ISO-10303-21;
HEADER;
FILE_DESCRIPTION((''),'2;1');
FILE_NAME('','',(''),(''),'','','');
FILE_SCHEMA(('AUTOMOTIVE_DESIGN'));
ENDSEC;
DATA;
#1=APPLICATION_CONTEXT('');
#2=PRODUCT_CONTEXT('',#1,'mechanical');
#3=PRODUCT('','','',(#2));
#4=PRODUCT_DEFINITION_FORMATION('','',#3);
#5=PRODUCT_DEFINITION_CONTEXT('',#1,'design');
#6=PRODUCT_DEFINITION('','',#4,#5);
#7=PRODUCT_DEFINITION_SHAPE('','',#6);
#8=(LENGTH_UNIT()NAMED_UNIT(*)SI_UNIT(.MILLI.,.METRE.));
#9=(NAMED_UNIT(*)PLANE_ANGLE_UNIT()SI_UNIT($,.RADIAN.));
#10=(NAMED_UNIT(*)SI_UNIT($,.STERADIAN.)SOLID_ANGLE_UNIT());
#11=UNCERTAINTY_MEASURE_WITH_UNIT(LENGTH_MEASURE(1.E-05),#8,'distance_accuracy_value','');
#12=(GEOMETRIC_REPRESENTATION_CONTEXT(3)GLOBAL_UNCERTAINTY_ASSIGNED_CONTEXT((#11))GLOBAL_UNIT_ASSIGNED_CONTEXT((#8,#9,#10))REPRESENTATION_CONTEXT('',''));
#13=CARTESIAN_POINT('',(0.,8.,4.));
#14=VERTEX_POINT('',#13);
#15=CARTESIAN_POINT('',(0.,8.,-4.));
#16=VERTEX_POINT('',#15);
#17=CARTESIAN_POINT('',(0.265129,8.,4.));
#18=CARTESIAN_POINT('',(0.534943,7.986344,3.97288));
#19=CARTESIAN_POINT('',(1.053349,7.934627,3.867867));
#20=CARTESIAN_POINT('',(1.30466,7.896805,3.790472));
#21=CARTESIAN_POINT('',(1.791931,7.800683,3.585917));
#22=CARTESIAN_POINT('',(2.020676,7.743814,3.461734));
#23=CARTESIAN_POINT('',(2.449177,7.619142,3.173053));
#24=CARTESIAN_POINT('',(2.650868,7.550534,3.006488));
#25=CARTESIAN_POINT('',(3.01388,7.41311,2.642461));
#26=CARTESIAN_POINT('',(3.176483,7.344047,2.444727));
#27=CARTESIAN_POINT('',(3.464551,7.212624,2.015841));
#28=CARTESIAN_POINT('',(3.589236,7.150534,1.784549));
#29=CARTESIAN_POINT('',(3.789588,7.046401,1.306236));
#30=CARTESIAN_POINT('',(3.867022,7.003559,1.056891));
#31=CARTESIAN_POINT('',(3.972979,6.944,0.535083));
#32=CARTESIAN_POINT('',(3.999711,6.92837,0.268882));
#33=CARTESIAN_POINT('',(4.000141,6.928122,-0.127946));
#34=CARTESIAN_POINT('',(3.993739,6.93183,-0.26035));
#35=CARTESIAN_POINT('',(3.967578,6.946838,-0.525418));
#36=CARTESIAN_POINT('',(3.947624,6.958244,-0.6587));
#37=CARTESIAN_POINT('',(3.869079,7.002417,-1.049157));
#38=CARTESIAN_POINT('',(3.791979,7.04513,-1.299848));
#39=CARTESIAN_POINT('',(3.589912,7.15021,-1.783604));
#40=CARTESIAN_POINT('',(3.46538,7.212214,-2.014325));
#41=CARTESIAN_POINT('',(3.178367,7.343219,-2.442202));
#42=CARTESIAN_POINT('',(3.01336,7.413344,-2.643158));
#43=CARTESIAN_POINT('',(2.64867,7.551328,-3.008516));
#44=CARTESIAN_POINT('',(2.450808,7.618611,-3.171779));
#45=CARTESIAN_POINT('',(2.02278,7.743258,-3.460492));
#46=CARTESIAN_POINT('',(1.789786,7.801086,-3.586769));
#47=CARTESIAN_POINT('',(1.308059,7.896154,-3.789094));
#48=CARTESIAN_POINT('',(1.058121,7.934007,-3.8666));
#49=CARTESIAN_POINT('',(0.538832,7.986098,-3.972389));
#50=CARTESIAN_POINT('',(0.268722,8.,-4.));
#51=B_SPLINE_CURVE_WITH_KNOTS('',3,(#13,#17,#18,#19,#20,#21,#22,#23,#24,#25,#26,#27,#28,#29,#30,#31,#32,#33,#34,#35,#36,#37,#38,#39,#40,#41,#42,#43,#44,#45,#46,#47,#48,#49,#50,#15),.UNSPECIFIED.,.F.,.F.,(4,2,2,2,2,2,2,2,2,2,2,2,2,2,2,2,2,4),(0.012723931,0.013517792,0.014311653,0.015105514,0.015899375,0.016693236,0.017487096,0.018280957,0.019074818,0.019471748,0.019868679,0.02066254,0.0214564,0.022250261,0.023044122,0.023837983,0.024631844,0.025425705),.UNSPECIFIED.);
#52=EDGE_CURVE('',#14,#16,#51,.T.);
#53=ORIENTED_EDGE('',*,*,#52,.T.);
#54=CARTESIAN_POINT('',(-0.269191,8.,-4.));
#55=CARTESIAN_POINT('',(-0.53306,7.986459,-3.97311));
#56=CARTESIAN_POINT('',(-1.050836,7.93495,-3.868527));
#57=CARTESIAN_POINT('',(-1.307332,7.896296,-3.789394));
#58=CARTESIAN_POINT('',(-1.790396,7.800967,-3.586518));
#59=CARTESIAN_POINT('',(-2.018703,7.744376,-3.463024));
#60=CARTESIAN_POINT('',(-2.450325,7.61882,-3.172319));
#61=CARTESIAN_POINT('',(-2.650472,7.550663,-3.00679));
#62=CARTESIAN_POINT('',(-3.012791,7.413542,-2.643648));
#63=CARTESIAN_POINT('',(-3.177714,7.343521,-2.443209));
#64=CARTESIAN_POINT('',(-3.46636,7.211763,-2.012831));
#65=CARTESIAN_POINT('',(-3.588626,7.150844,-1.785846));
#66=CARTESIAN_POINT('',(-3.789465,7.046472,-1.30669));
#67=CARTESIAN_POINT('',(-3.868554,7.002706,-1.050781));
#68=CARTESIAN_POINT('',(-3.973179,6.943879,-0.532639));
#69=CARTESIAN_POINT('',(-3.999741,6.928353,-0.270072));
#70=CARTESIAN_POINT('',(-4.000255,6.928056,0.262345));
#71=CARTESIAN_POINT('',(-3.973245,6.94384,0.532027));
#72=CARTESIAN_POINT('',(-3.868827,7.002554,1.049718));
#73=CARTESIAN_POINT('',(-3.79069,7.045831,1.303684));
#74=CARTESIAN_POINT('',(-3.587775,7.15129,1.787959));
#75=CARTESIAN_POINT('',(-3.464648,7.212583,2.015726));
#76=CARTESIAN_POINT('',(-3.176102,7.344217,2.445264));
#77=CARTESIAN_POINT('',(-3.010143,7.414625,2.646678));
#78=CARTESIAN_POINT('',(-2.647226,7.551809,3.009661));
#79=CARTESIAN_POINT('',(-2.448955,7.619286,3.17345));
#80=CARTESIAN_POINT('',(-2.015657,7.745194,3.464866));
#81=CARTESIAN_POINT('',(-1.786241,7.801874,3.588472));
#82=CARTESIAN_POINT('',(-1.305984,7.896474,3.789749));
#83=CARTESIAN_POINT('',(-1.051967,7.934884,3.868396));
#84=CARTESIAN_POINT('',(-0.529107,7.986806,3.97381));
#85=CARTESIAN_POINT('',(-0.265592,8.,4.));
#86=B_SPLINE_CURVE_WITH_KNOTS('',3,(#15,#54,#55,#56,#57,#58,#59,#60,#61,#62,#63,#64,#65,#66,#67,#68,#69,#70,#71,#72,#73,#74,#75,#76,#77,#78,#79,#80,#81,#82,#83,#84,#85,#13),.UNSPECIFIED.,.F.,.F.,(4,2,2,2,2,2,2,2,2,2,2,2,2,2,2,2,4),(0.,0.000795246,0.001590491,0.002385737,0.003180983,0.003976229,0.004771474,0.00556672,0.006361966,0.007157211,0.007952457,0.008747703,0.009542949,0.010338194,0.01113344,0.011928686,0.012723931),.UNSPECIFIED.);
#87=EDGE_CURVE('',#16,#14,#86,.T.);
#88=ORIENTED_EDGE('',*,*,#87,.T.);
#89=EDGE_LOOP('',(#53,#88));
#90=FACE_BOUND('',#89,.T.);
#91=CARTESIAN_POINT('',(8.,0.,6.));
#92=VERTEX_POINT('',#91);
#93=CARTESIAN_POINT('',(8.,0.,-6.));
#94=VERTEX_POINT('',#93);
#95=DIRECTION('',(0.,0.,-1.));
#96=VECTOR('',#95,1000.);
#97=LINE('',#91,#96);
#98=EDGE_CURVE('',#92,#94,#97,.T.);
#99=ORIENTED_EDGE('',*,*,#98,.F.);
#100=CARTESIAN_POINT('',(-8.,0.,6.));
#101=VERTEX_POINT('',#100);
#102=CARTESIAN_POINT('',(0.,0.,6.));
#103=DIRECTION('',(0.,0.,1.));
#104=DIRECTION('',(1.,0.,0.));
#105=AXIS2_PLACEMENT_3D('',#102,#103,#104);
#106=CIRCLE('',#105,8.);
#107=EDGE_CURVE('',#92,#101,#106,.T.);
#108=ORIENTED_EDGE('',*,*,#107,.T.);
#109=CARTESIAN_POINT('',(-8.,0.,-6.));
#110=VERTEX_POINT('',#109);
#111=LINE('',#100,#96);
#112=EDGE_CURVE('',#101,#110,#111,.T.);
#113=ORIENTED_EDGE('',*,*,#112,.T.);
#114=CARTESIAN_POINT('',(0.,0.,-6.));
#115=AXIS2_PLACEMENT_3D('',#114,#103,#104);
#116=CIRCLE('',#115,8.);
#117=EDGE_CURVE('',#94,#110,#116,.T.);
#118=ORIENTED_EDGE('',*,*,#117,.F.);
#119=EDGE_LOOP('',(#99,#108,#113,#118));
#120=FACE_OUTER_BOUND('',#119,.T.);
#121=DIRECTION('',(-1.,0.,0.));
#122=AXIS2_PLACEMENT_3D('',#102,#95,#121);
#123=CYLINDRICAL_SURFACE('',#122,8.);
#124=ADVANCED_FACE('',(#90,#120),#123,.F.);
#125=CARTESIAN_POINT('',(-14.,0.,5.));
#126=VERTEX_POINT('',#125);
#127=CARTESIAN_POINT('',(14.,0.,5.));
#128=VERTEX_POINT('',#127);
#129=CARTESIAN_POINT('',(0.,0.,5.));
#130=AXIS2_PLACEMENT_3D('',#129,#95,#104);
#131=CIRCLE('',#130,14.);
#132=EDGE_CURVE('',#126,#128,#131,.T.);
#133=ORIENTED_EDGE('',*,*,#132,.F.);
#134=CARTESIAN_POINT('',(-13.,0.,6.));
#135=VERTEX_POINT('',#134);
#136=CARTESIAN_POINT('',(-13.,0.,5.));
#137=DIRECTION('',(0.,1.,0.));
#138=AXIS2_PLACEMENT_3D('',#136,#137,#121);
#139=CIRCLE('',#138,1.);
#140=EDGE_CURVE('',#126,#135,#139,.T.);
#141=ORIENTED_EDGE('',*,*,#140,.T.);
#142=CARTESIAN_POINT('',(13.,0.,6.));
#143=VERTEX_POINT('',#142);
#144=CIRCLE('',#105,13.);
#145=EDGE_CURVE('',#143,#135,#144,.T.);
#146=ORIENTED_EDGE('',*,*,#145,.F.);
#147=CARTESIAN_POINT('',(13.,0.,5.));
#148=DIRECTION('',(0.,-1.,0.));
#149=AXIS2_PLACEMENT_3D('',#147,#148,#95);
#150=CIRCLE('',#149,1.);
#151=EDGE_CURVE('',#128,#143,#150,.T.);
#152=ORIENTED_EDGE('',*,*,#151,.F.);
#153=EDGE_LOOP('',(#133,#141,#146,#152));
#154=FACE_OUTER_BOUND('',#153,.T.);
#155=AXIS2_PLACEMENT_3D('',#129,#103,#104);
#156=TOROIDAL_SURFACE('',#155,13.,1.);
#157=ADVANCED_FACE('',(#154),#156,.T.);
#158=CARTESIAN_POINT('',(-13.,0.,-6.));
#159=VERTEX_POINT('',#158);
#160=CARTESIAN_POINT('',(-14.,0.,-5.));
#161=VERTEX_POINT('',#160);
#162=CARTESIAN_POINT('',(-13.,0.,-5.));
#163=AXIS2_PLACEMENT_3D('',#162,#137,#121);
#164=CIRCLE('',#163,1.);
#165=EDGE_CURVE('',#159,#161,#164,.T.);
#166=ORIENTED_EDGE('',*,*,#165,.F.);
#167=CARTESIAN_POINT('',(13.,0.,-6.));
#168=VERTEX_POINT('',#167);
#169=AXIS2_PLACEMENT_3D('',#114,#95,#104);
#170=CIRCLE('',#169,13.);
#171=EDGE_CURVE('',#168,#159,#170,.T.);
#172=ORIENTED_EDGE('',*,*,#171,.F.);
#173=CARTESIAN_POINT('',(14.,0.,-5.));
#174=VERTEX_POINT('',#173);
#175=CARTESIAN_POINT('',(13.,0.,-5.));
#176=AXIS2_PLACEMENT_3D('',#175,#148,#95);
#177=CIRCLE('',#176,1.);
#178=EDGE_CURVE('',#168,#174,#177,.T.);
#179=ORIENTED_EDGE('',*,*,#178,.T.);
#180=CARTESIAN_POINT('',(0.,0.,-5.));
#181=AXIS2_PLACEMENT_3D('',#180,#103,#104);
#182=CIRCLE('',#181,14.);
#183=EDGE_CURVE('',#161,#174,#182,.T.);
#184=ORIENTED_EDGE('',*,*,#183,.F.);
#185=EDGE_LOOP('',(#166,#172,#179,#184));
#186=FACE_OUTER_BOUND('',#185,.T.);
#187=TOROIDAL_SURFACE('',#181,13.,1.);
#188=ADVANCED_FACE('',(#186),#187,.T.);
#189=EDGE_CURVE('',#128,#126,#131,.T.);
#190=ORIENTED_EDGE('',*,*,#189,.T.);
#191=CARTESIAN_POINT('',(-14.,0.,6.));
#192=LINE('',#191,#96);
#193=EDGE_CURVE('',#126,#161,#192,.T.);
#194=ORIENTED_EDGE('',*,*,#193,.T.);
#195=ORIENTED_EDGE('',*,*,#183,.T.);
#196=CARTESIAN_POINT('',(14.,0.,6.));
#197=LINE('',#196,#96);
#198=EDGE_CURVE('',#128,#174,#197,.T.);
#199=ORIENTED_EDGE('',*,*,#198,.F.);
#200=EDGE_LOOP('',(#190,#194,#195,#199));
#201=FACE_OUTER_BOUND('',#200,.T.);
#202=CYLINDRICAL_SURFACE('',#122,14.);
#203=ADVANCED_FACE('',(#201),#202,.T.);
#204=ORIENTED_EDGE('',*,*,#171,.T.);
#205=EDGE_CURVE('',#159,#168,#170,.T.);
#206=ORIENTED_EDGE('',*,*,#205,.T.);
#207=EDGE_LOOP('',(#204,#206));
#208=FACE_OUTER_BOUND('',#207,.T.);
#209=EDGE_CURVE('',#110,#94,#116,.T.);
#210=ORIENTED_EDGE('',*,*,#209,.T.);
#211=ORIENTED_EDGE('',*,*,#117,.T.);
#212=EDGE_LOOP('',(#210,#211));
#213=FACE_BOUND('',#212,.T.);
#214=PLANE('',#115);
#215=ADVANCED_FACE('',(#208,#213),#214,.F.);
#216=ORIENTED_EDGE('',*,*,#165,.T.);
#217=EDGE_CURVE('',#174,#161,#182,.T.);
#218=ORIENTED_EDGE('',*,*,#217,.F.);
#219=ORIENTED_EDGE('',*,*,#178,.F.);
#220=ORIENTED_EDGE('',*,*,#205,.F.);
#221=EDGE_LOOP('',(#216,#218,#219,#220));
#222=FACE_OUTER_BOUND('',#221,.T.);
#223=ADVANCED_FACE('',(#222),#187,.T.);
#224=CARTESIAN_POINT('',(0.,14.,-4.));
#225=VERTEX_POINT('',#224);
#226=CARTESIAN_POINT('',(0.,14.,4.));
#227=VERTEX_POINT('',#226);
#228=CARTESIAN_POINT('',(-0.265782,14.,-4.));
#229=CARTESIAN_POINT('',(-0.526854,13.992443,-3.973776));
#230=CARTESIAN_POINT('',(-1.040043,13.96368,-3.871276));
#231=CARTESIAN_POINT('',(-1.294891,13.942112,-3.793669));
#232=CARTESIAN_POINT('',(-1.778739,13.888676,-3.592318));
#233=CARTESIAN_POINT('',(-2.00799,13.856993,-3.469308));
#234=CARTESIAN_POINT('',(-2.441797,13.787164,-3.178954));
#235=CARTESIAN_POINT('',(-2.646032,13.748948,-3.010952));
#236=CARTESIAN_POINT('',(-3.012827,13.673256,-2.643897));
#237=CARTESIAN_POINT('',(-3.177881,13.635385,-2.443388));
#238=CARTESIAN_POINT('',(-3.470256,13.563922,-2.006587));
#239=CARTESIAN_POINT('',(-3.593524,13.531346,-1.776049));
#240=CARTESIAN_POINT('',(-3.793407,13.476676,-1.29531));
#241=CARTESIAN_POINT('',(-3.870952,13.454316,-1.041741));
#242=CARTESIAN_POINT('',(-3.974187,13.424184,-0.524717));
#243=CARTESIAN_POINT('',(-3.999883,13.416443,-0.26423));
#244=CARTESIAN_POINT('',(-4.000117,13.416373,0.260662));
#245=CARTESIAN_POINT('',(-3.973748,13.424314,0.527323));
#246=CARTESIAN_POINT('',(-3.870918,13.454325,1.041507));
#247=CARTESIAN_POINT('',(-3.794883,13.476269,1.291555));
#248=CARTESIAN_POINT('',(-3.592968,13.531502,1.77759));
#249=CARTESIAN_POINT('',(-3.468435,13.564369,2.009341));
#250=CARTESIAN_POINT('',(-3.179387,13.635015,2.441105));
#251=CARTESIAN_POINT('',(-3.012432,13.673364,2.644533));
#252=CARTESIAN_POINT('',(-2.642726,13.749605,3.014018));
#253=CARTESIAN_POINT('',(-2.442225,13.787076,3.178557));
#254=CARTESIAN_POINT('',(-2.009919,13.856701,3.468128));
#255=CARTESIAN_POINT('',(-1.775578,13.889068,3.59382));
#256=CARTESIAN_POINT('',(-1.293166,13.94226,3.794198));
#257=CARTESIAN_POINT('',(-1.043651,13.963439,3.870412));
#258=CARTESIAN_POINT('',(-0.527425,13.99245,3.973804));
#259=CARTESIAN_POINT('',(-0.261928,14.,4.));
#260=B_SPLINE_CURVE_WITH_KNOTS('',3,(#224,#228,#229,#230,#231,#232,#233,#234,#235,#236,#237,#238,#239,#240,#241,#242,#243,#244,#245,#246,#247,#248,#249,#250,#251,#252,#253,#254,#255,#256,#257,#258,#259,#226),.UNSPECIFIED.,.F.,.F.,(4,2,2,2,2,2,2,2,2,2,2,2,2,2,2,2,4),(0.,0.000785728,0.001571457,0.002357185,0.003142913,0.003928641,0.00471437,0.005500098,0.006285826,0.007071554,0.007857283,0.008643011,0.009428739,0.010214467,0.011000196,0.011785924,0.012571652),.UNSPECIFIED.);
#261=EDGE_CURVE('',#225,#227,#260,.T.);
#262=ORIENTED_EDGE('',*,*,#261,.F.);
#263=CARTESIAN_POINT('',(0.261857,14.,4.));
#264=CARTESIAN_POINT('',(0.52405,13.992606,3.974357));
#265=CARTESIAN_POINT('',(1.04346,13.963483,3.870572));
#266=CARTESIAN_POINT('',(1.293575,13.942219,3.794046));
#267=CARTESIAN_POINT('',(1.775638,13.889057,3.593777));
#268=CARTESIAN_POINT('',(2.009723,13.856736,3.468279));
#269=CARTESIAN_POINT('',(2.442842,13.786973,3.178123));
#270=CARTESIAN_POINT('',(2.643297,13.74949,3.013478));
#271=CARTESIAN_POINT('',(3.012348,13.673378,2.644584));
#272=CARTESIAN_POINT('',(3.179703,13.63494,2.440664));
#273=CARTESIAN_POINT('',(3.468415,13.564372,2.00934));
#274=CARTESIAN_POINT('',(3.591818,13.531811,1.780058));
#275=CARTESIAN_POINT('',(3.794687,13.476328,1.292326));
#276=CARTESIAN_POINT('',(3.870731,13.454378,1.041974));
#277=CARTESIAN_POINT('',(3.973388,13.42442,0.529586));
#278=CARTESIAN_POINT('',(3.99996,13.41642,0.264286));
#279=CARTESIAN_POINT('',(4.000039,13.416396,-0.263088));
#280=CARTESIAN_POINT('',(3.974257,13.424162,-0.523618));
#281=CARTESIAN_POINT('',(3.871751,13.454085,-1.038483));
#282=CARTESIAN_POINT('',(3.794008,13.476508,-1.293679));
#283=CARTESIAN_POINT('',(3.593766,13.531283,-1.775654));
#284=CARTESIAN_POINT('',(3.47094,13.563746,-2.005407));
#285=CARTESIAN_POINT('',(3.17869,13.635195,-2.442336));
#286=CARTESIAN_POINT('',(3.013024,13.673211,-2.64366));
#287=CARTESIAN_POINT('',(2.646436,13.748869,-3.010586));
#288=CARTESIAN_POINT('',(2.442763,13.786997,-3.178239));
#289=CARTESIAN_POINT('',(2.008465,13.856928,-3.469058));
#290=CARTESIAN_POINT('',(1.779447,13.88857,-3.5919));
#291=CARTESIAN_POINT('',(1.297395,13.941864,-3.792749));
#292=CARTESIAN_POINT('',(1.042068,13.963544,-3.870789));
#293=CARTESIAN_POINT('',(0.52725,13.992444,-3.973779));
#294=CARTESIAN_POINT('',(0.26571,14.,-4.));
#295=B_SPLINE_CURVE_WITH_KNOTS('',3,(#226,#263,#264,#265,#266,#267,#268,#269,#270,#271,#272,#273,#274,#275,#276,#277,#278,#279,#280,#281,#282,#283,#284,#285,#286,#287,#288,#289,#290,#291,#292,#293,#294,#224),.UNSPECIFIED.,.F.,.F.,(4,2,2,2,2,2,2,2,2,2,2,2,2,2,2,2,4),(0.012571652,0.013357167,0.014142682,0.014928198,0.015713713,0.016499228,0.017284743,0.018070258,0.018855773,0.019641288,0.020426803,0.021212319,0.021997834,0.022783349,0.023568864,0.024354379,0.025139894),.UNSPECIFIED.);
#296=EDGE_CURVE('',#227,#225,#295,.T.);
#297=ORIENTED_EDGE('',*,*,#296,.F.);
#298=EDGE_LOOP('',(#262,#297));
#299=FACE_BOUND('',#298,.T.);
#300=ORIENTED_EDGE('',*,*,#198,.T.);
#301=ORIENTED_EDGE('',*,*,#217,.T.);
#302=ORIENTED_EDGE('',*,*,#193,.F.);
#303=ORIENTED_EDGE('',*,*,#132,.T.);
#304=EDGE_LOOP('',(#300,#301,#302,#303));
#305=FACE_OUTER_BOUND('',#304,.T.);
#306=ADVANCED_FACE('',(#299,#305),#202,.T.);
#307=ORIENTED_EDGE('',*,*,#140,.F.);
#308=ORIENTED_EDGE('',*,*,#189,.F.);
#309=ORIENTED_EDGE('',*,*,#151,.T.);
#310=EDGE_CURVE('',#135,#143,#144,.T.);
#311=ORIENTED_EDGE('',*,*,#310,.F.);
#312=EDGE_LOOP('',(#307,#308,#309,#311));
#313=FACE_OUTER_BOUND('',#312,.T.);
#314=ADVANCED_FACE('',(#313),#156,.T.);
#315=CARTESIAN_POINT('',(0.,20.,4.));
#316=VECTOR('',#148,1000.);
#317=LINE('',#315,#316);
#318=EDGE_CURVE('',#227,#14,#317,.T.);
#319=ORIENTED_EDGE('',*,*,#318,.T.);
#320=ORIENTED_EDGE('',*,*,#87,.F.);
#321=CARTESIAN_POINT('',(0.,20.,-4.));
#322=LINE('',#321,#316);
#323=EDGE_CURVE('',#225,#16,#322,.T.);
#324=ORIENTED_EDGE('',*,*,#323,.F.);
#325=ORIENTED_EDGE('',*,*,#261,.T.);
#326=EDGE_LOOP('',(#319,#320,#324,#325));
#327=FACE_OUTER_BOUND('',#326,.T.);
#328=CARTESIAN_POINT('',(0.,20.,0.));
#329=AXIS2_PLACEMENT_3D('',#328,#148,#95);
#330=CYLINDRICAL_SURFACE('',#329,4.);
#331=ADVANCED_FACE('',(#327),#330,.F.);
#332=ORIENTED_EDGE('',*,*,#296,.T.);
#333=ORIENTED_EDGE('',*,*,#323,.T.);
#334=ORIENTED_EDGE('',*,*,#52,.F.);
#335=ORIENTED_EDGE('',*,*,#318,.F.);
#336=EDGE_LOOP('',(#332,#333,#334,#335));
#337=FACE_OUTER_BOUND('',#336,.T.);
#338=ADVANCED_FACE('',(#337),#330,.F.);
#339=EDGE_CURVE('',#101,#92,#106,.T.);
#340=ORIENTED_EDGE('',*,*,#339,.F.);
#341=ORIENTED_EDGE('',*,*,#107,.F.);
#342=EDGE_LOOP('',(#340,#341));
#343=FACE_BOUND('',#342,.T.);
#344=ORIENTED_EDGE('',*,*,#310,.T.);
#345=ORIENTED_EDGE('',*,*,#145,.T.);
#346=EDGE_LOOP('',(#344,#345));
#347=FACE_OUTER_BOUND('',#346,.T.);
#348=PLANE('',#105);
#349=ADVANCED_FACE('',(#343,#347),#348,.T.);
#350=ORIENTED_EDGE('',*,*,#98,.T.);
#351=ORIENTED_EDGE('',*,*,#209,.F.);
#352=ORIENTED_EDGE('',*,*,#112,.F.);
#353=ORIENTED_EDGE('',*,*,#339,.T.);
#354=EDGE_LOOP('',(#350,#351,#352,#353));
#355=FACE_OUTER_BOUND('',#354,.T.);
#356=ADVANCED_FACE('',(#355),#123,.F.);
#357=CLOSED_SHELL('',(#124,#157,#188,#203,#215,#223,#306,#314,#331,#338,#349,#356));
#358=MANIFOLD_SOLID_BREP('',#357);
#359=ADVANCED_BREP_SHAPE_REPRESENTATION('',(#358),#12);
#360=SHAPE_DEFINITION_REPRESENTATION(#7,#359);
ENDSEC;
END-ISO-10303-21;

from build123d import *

# Parameters (mm, degrees)
SKETCH1_R           = 14
SKETCH1_R_2         = 8
BOSS_EXTRUDE1_DEPTH = 6
FILLET1_R           = 1
SKETCH2_R           = 4
CUT_EXTRUDE1_DEPTH  = 20


with BuildPart() as part:
    # Sketch1 → Boss-Extrude1 (new, symmetric)
    with BuildSketch(Plane.XY):
        Circle(SKETCH1_R)
        Circle(SKETCH1_R_2, mode=Mode.SUBTRACT)
    extrude(amount=BOSS_EXTRUDE1_DEPTH, both=True)

    # Fillet1
    fillet1_edges = [part.edges().sort_by_distance(p)[0] for p in [
        (-14, 0, -6),
        (-14, 0, 6),
    ]]
    fillet(fillet1_edges, radius=FILLET1_R)

    # Sketch2 → Cut-Extrude1 (cut)
    with BuildSketch(Plane(origin=(0, 0, 0), x_dir=(1, 0, 0), z_dir=(0, 1, 0))):
        with Locations(Location((0, 0, 0), (0, 0, 90))):
            Circle(SKETCH2_R)
    extrude(amount=CUT_EXTRUDE1_DEPTH, mode=Mode.SUBTRACT)


solid = part.part
